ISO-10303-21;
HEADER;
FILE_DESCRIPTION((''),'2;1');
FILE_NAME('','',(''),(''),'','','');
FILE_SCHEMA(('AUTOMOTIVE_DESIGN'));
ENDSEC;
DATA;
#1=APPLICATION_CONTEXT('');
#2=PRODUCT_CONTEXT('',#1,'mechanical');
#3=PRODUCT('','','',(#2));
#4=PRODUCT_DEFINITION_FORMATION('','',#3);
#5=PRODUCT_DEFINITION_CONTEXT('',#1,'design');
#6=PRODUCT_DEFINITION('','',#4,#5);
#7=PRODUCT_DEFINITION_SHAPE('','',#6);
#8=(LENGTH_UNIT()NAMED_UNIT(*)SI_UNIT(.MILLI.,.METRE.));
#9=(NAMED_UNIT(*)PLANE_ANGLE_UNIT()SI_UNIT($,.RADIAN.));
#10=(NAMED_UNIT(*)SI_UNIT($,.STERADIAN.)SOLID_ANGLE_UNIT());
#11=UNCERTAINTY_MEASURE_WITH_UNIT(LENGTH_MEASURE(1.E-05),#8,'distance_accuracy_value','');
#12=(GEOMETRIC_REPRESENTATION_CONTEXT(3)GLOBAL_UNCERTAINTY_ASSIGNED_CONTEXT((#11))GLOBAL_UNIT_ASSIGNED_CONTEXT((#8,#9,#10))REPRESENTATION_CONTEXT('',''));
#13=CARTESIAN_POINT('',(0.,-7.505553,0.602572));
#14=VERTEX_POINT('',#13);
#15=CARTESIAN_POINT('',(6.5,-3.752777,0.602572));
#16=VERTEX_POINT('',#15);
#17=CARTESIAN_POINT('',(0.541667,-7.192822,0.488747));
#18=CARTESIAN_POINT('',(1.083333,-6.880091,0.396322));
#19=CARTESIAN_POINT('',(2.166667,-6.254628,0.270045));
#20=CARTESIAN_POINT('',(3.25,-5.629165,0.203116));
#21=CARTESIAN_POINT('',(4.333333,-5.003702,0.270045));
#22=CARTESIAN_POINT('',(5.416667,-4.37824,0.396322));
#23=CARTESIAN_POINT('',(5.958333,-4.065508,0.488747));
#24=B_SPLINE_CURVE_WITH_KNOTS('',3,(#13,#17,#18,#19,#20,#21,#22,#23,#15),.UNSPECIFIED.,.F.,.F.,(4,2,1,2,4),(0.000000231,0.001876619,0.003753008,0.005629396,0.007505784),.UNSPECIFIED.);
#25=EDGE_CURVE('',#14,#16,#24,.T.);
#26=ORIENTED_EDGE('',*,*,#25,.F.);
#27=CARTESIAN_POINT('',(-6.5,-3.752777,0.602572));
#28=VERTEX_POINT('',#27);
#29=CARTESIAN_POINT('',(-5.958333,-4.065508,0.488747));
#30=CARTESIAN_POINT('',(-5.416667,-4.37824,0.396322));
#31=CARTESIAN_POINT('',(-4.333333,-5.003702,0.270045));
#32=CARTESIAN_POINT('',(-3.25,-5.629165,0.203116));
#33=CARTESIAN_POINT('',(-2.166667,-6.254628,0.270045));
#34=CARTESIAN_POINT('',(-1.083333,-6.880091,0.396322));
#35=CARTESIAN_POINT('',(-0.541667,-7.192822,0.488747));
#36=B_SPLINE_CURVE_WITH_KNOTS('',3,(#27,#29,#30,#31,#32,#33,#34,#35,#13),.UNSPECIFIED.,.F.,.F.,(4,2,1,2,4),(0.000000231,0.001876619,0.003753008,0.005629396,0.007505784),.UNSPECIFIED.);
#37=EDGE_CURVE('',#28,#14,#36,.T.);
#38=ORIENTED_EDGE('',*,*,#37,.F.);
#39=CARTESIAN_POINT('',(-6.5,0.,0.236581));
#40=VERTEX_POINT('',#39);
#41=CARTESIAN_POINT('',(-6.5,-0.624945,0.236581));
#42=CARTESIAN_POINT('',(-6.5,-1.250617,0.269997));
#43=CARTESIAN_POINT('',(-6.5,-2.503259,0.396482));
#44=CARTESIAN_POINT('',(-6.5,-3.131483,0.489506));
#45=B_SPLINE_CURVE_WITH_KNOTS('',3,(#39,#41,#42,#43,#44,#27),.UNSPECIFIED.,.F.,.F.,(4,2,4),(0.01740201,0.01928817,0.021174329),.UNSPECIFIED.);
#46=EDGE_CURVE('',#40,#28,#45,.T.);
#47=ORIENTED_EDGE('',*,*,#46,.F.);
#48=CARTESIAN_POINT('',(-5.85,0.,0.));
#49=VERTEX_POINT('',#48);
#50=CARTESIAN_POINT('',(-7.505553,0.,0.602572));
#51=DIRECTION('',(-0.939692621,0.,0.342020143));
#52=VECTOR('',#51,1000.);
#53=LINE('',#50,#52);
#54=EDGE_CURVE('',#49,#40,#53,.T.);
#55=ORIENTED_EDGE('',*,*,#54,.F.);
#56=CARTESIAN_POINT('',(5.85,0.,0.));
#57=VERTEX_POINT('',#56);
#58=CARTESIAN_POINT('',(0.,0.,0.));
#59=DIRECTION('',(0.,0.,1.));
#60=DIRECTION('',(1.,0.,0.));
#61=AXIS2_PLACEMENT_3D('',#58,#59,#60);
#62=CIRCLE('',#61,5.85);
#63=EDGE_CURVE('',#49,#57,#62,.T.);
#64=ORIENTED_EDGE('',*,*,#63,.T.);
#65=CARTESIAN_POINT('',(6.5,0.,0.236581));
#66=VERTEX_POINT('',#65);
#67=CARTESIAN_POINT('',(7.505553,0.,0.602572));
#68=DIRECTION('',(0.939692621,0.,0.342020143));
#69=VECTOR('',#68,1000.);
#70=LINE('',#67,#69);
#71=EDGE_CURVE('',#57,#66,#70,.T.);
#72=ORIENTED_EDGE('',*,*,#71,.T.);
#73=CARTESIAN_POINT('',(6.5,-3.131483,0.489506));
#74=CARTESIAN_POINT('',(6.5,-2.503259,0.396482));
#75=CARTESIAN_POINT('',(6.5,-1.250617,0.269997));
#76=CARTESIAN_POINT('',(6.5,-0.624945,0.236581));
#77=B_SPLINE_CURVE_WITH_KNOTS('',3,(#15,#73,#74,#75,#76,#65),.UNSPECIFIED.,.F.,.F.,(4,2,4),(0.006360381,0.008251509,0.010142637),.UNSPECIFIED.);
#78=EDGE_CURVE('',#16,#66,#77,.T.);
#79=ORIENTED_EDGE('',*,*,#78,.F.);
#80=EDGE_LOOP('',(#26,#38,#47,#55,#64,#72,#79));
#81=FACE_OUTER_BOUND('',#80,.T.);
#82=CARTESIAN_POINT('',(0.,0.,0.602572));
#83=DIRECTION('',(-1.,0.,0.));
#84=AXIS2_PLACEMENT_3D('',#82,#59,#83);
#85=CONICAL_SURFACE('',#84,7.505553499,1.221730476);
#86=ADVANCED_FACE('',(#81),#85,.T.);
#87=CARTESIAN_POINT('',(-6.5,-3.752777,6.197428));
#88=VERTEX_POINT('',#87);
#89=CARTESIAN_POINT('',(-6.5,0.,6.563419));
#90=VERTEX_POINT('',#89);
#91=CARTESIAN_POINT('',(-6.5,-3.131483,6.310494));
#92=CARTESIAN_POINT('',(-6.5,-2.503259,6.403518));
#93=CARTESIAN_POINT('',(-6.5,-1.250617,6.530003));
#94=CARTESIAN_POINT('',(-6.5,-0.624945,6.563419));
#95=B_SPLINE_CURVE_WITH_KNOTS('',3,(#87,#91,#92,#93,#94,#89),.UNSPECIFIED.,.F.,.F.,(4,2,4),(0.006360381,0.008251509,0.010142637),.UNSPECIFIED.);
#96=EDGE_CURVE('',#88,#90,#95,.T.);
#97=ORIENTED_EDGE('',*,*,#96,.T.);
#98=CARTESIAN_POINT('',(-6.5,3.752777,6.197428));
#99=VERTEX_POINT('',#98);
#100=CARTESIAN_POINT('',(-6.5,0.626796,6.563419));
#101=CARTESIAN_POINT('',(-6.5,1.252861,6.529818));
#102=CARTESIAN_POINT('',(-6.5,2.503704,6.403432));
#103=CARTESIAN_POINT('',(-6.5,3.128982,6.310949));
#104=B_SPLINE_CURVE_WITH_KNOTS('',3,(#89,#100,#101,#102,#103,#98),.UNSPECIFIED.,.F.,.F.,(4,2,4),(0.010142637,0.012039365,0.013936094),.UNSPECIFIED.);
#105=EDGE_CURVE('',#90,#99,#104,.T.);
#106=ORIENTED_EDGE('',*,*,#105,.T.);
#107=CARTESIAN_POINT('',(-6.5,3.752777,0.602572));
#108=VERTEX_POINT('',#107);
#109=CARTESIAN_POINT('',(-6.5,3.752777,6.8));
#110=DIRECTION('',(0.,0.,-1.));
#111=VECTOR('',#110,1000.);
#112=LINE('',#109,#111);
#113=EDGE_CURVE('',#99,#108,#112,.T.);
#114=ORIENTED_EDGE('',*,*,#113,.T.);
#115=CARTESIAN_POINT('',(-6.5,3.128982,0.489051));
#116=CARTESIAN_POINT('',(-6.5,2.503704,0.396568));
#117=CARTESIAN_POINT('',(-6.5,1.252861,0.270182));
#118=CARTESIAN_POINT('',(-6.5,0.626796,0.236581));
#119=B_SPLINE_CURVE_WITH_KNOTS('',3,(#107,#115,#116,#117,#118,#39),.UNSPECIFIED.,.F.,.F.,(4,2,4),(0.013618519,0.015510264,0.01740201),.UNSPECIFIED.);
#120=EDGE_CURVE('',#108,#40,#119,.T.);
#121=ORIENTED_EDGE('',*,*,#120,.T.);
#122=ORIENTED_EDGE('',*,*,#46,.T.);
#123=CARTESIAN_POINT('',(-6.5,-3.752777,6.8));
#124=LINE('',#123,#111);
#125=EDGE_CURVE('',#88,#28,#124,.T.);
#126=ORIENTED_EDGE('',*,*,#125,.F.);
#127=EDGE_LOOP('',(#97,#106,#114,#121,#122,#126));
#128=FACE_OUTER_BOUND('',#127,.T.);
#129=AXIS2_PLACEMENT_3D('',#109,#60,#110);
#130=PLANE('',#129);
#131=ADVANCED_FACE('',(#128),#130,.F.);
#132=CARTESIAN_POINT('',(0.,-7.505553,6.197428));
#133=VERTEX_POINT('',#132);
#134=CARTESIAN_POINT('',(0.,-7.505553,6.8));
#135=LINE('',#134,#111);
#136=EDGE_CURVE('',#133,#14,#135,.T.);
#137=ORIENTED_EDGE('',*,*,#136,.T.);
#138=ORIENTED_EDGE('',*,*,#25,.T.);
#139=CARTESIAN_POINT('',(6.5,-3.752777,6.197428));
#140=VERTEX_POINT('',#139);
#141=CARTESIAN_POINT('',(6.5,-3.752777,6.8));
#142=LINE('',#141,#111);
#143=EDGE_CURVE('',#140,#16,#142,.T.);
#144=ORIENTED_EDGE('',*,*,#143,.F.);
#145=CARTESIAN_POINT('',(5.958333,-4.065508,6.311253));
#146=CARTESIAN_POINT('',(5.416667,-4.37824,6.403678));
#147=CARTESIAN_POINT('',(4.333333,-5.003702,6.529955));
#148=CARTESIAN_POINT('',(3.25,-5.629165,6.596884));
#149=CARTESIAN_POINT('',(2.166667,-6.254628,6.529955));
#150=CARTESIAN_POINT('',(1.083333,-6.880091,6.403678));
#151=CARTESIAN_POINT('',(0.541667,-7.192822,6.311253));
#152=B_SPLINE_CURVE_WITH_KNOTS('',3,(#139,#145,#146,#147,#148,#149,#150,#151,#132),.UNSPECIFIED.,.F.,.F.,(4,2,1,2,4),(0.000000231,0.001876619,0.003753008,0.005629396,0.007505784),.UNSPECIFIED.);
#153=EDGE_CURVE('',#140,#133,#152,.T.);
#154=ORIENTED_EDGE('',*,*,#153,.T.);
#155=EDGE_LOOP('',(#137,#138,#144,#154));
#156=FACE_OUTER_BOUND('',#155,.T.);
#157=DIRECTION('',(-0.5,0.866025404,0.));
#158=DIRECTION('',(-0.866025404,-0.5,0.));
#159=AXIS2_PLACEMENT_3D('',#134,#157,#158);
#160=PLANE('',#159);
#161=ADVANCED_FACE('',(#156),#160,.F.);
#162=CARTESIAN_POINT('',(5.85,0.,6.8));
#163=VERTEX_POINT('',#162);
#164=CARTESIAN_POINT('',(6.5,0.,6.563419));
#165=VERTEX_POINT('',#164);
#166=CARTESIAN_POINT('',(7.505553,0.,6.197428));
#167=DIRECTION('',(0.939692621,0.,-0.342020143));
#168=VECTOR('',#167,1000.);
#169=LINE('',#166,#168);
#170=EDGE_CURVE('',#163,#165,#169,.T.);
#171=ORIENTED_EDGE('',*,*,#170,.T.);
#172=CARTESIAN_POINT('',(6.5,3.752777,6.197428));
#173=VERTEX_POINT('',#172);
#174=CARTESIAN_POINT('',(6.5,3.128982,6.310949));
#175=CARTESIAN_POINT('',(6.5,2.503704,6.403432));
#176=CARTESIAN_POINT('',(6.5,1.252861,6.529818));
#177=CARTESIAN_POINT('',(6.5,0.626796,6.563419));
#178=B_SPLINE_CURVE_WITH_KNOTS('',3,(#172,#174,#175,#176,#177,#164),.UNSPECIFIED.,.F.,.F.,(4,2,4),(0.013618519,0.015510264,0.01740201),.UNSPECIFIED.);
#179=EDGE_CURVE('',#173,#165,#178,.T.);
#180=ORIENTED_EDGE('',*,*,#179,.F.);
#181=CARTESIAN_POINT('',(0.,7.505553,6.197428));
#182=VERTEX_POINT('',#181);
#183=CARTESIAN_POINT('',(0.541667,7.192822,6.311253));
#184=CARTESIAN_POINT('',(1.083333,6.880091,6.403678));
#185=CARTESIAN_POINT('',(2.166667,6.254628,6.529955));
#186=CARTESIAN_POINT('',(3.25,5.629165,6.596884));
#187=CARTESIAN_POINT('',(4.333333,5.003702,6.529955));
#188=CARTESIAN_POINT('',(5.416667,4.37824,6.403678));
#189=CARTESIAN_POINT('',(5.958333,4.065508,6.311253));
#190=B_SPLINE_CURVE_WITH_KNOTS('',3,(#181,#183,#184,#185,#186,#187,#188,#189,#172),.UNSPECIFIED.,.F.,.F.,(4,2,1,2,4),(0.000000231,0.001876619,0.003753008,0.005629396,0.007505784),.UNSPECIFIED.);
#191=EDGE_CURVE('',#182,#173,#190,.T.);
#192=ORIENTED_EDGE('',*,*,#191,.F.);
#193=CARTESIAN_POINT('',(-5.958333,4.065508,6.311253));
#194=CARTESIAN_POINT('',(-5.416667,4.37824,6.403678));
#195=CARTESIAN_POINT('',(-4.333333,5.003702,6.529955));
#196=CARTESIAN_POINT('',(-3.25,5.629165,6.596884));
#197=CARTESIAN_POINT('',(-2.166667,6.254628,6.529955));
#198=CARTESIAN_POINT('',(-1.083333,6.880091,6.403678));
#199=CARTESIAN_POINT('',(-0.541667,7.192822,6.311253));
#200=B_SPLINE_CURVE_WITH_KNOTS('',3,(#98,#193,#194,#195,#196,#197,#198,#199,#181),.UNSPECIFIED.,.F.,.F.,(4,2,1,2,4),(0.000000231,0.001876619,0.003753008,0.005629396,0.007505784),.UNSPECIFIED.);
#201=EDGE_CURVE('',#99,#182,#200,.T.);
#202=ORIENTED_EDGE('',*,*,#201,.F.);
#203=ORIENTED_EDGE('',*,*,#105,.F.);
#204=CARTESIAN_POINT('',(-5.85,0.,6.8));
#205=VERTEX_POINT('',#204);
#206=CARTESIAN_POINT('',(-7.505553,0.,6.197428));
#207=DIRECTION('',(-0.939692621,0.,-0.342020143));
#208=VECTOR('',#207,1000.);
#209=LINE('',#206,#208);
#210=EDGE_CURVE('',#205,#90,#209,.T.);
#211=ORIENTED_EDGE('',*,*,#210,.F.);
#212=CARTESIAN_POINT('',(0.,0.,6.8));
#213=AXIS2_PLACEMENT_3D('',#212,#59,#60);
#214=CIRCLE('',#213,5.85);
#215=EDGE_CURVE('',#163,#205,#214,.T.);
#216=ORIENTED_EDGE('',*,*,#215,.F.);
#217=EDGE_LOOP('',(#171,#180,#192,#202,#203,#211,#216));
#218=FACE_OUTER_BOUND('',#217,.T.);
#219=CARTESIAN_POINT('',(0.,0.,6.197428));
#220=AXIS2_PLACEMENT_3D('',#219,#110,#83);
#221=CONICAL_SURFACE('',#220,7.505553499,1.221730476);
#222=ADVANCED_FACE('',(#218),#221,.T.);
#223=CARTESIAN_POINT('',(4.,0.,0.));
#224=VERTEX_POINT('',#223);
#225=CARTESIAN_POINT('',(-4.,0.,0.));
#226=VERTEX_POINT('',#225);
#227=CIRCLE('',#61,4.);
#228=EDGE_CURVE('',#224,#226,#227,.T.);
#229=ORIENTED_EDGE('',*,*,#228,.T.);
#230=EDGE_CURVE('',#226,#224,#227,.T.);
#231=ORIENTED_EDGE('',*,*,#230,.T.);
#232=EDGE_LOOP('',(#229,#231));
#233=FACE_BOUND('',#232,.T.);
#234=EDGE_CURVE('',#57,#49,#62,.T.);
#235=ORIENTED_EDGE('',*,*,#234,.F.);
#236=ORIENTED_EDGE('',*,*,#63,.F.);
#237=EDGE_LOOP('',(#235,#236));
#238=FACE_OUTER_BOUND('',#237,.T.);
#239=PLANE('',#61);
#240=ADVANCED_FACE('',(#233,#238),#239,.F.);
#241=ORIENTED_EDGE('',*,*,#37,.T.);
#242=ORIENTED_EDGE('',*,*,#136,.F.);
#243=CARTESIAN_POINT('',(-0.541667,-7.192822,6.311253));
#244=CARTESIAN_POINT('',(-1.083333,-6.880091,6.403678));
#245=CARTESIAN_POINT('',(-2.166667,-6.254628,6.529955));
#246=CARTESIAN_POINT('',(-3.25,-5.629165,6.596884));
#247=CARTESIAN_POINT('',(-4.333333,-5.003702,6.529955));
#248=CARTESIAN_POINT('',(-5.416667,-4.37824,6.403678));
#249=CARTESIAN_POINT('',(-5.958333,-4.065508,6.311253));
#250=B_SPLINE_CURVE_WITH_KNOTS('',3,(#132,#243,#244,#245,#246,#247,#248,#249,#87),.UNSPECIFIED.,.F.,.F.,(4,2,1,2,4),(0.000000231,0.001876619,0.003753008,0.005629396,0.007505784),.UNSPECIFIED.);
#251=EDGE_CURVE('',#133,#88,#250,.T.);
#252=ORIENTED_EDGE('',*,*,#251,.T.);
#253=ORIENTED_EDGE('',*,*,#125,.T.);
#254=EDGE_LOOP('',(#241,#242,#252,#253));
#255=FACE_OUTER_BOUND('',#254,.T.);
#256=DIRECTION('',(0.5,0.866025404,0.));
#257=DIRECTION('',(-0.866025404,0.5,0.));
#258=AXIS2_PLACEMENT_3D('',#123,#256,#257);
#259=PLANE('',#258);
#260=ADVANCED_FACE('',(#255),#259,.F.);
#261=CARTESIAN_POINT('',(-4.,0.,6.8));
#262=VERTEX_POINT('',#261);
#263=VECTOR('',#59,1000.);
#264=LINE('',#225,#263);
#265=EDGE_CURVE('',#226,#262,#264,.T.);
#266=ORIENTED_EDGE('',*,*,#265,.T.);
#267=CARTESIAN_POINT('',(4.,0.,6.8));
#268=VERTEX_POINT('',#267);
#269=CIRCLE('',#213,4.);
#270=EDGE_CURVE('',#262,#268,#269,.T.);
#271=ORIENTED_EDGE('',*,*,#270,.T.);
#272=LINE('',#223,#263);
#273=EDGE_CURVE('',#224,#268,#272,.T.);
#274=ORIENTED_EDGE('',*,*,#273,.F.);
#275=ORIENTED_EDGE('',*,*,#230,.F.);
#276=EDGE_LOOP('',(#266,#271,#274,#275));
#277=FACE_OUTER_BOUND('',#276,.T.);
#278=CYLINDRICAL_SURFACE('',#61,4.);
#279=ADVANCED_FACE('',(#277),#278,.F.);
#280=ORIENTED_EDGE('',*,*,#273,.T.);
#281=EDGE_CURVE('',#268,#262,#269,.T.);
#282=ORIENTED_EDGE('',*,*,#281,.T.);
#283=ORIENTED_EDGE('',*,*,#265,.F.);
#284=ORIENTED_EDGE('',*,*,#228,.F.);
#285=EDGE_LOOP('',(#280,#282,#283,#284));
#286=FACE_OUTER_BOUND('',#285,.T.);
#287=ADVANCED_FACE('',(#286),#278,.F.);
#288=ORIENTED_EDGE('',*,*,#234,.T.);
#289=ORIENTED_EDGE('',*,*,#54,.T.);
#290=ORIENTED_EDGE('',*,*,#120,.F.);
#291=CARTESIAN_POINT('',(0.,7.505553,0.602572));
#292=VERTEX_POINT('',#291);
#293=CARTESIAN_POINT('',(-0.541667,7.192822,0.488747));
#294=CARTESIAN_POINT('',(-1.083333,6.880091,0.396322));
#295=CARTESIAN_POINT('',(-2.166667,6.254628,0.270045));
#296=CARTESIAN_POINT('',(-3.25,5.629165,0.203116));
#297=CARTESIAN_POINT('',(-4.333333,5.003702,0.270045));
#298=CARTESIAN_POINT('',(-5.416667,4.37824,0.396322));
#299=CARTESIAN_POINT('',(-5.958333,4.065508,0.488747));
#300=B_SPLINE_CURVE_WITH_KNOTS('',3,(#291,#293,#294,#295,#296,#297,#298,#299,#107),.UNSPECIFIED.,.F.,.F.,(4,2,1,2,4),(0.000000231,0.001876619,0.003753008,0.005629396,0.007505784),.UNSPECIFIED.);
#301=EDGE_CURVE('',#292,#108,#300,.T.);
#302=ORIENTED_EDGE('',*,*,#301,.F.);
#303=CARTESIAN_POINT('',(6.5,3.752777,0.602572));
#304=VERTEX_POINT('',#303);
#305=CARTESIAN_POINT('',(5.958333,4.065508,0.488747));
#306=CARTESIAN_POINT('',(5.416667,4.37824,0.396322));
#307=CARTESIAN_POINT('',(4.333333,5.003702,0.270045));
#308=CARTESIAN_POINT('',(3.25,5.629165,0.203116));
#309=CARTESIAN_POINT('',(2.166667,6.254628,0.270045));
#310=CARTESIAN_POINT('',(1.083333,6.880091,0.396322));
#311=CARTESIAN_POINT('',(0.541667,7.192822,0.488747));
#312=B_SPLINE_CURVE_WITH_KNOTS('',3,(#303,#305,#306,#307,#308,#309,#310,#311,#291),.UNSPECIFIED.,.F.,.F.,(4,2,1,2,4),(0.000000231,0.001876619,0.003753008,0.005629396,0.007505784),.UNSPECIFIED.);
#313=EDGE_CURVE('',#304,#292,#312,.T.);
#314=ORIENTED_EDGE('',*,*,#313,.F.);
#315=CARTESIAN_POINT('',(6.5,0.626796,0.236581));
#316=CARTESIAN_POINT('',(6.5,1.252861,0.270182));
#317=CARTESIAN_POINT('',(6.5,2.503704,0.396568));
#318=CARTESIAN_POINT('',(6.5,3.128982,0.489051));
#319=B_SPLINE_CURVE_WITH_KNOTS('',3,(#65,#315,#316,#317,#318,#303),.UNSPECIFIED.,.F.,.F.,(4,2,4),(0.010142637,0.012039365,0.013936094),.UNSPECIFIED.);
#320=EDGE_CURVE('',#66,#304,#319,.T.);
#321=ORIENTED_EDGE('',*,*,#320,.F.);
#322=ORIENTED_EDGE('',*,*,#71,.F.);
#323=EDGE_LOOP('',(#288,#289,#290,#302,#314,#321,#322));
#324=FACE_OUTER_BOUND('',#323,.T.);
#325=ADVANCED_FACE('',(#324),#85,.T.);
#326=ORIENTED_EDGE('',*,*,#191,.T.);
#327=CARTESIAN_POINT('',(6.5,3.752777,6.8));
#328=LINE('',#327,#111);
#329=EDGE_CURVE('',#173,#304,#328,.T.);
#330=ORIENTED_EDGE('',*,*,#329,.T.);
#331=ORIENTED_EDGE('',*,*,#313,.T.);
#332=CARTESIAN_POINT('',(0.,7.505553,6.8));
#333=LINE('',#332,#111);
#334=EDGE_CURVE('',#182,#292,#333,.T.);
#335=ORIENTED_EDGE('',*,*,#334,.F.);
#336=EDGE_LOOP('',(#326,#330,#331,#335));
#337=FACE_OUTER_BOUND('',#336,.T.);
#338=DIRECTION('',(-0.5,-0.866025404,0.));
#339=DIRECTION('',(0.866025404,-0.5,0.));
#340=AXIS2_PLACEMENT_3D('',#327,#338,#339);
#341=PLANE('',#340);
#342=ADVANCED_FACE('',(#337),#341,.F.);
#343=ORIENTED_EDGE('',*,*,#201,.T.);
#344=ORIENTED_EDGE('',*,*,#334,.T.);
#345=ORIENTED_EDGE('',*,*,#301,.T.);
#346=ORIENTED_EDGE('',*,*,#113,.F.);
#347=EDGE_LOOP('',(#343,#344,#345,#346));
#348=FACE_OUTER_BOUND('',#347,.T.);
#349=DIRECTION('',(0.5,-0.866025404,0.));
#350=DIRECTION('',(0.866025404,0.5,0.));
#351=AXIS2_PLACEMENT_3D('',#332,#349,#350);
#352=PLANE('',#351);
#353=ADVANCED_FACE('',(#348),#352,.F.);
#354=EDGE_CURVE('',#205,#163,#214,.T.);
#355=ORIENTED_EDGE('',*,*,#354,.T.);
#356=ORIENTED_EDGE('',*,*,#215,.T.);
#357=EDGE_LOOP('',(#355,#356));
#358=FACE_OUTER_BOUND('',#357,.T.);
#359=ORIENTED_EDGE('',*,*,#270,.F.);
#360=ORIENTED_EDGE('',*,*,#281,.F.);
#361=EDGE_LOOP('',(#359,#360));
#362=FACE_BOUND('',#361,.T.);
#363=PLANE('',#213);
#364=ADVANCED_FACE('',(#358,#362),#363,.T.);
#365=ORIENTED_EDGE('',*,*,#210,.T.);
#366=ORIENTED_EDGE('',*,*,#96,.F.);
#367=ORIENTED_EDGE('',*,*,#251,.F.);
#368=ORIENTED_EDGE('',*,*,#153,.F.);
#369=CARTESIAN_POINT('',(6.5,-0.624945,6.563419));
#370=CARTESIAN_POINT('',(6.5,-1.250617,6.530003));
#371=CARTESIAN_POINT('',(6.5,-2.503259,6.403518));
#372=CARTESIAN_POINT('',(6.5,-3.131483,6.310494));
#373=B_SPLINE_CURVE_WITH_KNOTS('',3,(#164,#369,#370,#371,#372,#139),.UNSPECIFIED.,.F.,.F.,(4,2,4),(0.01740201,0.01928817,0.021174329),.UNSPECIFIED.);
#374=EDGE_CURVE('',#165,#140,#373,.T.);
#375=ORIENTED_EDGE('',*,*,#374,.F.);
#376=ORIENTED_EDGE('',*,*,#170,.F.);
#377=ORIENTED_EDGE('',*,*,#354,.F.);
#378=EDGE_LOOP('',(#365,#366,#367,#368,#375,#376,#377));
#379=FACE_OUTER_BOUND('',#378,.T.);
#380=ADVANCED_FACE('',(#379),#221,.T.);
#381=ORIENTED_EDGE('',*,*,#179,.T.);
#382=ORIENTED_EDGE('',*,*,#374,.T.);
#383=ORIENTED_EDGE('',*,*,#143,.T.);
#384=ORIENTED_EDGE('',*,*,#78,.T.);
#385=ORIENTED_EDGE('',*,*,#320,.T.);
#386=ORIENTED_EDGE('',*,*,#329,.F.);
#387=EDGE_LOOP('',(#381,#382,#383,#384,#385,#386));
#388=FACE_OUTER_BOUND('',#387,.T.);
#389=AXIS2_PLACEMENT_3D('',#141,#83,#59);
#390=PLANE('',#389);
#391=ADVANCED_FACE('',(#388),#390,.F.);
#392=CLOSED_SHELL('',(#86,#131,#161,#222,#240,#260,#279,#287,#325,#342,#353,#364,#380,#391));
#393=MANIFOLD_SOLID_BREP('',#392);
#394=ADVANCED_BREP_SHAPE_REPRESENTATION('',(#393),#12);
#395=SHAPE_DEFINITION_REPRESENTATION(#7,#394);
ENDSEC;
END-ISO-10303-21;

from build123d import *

# Parameters (mm, degrees)
EXTRUDE_1_DEPTH     = 6.8
SKETCH_5_R          = 4
CUT_EXTRUDE_1_DEPTH = 13.03425666


with BuildPart() as part:
    # 草图1 → 凸台-拉伸1 (new body)
    with BuildSketch(Plane.XY):
        Polygon((0, 7.505553499), (-6.5, 3.75277675), (-6.5, -3.75277675), (0, -7.505553499), (6.5, -3.75277675), (6.5, 3.75277675), align=None)
    extrude(amount=EXTRUDE_1_DEPTH)

    # 草图4 → 切除-旋转1 (revolve, cut)
    with BuildSketch(Plane(origin=(0, 0, 0), x_dir=(0, 0, -1), z_dir=(1, 0, 0)), mode=Mode.PRIVATE) as cut_revolve_1_sk:
        Polygon((-6.8, -5.85), (-6.197427805, -7.505553499), (-6.8, -7.505553499), align=None)
    cut_revolve_1 = revolve(cut_revolve_1_sk.sketch.rotate(Axis((0, 0, 6.8), (0, 0, -1)), 119.999999984), axis=Axis((0, 0, 6.8), (0, 0, -1)), mode=Mode.SUBTRACT)

    # 镜向1: 切除-旋转1 across plane
    add(cut_revolve_1.mirror(Plane.XY.offset(3.4)), mode=Mode.SUBTRACT)

    # 草图5 → 切除-拉伸1 (cut, through all)
    with BuildSketch(Plane.XY.offset(6.8)):
        Circle(SKETCH_5_R)
    extrude(amount=-CUT_EXTRUDE_1_DEPTH, mode=Mode.SUBTRACT)


solid = part.part
